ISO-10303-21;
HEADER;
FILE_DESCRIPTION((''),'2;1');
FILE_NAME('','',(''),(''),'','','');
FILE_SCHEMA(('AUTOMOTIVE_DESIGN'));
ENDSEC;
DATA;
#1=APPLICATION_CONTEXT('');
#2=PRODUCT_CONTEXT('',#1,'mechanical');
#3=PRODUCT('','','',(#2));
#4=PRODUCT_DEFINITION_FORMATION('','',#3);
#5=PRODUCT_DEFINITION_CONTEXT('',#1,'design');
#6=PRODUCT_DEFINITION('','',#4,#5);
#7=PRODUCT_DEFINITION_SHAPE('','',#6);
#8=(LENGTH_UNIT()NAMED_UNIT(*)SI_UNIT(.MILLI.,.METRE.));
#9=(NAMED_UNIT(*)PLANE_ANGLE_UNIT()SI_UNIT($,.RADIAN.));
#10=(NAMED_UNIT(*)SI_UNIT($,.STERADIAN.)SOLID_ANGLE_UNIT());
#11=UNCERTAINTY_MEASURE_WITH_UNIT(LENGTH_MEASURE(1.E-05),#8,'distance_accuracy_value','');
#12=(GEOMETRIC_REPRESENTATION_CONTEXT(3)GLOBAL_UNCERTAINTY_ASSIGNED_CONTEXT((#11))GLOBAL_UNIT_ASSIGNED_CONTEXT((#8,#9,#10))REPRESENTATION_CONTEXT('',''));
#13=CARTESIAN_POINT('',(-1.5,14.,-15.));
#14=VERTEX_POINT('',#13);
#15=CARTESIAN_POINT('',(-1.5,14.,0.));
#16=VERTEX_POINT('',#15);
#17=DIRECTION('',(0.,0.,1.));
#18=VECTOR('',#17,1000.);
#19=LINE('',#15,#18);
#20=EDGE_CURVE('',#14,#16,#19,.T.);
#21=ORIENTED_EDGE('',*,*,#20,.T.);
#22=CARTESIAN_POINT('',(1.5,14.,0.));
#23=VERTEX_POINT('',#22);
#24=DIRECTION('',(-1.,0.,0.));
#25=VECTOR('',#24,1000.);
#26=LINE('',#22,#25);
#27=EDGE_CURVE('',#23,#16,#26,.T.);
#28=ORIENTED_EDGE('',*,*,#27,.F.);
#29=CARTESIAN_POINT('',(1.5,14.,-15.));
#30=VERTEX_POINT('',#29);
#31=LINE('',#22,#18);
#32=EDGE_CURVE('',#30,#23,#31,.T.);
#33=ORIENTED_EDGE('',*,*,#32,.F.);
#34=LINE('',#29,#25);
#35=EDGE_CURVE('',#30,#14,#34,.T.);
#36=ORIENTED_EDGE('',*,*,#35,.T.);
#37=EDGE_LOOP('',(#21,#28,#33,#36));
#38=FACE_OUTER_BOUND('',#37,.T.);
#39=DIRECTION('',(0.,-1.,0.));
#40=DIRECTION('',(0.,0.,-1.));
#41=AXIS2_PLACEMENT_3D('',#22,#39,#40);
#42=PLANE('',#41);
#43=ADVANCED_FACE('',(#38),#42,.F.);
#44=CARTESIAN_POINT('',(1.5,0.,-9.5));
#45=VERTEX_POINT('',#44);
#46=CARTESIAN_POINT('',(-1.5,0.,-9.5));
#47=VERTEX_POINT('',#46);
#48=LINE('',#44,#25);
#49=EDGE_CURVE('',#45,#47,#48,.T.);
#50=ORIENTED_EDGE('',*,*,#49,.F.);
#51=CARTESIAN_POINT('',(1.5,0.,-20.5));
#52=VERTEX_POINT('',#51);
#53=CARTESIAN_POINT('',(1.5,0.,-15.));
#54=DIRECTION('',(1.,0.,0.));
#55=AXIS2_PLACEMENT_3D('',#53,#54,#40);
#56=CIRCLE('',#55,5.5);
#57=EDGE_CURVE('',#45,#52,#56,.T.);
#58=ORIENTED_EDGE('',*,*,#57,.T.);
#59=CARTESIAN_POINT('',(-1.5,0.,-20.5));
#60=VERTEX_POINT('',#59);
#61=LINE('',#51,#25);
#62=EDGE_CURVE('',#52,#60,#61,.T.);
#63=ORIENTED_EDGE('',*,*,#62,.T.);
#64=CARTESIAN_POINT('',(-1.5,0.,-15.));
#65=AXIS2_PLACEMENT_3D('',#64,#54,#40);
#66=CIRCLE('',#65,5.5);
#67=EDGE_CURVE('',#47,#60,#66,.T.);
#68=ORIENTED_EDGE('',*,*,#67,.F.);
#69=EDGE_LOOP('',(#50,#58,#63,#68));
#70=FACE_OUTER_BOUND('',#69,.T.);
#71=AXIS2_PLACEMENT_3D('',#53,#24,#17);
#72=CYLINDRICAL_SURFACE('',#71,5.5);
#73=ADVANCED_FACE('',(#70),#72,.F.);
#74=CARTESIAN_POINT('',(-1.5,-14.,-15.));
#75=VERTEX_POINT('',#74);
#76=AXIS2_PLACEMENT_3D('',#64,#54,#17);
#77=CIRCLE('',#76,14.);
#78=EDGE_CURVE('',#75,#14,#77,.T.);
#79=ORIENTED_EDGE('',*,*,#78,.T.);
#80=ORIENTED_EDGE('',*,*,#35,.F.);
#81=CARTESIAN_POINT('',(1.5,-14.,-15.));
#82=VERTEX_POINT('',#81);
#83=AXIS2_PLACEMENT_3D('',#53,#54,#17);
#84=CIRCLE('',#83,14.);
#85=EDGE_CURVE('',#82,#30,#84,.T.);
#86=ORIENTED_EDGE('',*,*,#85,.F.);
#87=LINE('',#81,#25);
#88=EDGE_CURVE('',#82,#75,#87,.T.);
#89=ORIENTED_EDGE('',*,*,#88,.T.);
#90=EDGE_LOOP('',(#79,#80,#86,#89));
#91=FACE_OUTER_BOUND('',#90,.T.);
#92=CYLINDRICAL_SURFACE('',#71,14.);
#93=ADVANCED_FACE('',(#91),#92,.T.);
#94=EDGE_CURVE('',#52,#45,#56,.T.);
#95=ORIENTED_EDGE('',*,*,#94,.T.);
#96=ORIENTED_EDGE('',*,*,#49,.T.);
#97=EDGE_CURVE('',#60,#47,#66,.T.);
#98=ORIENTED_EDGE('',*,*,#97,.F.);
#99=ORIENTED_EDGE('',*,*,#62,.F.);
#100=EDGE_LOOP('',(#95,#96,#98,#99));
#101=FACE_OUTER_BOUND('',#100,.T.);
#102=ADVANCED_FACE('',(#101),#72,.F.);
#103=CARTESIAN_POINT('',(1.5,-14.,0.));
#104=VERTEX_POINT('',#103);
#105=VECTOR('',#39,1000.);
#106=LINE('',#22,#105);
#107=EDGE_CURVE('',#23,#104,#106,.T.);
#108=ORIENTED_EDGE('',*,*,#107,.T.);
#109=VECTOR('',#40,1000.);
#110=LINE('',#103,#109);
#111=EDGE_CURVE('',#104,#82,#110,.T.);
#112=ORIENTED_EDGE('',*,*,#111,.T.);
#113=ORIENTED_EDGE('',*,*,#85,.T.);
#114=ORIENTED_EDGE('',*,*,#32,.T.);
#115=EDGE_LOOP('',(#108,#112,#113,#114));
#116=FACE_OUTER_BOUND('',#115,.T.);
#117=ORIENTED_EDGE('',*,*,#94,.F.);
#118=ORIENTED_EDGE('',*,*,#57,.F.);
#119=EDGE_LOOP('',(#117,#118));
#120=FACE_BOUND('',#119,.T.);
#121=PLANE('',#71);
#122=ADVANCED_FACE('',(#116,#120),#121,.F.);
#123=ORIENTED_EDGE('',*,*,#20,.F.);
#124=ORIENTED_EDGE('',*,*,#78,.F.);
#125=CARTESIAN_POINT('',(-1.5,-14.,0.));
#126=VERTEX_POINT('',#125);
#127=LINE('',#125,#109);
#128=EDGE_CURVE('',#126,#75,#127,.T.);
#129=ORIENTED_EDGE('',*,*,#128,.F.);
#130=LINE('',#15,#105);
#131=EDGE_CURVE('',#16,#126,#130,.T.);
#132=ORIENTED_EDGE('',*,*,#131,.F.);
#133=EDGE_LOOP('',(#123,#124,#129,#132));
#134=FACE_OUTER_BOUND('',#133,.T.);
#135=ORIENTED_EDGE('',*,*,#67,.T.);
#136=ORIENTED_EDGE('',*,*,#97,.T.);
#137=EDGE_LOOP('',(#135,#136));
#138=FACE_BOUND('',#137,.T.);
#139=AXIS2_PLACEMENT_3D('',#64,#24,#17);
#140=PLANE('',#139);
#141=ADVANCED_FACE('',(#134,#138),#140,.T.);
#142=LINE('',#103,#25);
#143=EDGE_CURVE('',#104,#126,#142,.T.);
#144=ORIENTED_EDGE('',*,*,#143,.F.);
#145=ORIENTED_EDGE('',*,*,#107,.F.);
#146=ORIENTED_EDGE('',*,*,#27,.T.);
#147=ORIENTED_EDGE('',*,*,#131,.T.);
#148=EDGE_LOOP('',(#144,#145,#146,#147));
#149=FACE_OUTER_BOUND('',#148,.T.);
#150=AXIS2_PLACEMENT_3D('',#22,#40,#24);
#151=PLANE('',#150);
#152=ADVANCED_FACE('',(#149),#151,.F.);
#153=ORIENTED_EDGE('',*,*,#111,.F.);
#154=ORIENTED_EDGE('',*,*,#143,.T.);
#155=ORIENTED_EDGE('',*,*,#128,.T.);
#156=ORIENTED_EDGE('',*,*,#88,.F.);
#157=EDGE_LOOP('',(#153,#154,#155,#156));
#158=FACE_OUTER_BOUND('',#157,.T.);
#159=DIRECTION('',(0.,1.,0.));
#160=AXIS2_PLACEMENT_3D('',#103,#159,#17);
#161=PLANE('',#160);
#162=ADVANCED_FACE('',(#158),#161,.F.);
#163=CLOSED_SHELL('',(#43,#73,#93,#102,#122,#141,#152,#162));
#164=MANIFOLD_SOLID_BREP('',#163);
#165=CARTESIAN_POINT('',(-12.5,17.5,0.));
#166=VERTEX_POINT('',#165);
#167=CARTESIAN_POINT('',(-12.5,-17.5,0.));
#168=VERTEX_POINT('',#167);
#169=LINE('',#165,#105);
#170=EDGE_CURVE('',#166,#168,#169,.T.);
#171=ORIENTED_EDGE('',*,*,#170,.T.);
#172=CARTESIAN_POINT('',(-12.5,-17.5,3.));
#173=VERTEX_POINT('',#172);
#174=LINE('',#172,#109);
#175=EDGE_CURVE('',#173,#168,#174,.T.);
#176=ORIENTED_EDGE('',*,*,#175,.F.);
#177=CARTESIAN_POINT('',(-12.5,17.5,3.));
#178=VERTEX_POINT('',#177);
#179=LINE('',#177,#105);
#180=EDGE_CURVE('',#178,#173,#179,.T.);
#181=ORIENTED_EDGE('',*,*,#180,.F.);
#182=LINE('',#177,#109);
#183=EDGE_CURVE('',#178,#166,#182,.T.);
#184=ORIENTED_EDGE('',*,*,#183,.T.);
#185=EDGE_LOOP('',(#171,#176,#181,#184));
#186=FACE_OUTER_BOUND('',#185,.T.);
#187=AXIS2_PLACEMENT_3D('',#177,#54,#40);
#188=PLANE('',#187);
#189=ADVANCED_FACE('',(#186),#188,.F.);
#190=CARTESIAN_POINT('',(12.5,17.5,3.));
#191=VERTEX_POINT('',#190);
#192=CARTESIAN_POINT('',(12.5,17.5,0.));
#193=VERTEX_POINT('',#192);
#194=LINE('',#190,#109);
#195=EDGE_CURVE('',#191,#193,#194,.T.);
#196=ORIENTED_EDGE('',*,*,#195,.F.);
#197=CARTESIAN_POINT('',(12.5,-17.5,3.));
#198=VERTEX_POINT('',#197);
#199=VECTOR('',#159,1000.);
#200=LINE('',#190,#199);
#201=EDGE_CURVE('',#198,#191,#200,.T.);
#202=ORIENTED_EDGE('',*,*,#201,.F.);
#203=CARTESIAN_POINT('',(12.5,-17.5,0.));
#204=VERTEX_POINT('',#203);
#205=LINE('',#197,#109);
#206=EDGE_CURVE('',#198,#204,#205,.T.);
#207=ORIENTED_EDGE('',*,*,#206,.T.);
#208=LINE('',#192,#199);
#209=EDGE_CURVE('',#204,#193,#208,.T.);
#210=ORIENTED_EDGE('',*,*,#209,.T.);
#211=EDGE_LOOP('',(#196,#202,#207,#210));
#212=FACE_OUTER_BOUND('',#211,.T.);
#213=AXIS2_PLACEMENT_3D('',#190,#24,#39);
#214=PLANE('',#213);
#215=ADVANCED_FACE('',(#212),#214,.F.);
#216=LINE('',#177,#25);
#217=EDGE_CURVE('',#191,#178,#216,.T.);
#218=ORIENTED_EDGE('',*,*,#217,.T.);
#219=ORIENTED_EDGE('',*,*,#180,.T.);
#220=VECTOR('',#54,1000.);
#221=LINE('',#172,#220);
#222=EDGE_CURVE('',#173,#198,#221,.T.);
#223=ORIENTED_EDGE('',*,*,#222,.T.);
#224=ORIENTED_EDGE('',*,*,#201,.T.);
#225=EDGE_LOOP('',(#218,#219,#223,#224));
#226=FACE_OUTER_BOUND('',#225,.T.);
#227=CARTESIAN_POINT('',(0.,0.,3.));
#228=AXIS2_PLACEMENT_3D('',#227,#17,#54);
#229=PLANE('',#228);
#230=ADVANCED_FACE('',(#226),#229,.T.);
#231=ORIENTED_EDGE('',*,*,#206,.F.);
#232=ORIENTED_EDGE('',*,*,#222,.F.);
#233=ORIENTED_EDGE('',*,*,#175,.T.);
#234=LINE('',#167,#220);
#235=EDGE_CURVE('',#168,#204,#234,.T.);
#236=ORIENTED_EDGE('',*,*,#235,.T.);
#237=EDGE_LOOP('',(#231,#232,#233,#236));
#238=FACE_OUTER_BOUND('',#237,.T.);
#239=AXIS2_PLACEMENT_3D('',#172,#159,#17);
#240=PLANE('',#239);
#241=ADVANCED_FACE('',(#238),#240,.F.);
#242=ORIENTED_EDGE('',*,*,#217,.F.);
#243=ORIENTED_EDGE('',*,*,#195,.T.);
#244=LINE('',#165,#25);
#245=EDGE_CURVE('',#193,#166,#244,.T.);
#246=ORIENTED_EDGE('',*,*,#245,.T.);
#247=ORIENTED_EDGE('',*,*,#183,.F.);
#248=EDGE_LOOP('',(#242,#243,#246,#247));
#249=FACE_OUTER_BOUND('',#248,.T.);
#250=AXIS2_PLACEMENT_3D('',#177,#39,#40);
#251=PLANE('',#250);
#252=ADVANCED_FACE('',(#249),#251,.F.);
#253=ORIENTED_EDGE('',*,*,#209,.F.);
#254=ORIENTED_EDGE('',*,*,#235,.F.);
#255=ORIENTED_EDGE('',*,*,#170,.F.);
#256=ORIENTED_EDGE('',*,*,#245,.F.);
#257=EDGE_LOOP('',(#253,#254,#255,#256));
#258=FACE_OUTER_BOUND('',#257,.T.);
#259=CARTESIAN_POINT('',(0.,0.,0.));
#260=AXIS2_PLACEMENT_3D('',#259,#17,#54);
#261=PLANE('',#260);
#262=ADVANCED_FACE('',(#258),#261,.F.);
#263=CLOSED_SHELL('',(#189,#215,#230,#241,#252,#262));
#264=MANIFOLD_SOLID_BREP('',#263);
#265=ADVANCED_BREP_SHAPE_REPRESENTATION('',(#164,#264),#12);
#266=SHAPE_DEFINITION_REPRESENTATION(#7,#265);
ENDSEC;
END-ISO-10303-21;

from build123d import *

# Parameters (mm, degrees)
SKETCH_1_W      = 25
SKETCH_1_H      = 35
EXTRUDE_1_DEPTH = 3
SKETCH_2_R      = 5.5
EXTRUDE_2_DEPTH = 1.5


with BuildPart() as part:
    # 草图1 → 凸台-拉伸1 (new body)
    with BuildSketch(Plane.XY):
        Rectangle(SKETCH_1_W, SKETCH_1_H)
    extrude(amount=EXTRUDE_1_DEPTH)


with BuildPart() as body_2:
    # 草图2 → 凸台-拉伸2 (new, symmetric)
    with BuildSketch(Plane(origin=(0, 0, 0), x_dir=(0, 0, -1), z_dir=(1, 0, 0))):
        with BuildLine():
            Line((0, 14), (15, 14))
            ThreePointArc((15, 14), (29, 0), (15, -14))
            Line((15, -14), (0, -14))
            Line((0, -14), (0, 14))
        make_face()
        with Locations((15, 0)):
            Circle(SKETCH_2_R, mode=Mode.SUBTRACT)
    extrude(amount=EXTRUDE_2_DEPTH, both=True)


solid = Compound([part.part, body_2.part])
